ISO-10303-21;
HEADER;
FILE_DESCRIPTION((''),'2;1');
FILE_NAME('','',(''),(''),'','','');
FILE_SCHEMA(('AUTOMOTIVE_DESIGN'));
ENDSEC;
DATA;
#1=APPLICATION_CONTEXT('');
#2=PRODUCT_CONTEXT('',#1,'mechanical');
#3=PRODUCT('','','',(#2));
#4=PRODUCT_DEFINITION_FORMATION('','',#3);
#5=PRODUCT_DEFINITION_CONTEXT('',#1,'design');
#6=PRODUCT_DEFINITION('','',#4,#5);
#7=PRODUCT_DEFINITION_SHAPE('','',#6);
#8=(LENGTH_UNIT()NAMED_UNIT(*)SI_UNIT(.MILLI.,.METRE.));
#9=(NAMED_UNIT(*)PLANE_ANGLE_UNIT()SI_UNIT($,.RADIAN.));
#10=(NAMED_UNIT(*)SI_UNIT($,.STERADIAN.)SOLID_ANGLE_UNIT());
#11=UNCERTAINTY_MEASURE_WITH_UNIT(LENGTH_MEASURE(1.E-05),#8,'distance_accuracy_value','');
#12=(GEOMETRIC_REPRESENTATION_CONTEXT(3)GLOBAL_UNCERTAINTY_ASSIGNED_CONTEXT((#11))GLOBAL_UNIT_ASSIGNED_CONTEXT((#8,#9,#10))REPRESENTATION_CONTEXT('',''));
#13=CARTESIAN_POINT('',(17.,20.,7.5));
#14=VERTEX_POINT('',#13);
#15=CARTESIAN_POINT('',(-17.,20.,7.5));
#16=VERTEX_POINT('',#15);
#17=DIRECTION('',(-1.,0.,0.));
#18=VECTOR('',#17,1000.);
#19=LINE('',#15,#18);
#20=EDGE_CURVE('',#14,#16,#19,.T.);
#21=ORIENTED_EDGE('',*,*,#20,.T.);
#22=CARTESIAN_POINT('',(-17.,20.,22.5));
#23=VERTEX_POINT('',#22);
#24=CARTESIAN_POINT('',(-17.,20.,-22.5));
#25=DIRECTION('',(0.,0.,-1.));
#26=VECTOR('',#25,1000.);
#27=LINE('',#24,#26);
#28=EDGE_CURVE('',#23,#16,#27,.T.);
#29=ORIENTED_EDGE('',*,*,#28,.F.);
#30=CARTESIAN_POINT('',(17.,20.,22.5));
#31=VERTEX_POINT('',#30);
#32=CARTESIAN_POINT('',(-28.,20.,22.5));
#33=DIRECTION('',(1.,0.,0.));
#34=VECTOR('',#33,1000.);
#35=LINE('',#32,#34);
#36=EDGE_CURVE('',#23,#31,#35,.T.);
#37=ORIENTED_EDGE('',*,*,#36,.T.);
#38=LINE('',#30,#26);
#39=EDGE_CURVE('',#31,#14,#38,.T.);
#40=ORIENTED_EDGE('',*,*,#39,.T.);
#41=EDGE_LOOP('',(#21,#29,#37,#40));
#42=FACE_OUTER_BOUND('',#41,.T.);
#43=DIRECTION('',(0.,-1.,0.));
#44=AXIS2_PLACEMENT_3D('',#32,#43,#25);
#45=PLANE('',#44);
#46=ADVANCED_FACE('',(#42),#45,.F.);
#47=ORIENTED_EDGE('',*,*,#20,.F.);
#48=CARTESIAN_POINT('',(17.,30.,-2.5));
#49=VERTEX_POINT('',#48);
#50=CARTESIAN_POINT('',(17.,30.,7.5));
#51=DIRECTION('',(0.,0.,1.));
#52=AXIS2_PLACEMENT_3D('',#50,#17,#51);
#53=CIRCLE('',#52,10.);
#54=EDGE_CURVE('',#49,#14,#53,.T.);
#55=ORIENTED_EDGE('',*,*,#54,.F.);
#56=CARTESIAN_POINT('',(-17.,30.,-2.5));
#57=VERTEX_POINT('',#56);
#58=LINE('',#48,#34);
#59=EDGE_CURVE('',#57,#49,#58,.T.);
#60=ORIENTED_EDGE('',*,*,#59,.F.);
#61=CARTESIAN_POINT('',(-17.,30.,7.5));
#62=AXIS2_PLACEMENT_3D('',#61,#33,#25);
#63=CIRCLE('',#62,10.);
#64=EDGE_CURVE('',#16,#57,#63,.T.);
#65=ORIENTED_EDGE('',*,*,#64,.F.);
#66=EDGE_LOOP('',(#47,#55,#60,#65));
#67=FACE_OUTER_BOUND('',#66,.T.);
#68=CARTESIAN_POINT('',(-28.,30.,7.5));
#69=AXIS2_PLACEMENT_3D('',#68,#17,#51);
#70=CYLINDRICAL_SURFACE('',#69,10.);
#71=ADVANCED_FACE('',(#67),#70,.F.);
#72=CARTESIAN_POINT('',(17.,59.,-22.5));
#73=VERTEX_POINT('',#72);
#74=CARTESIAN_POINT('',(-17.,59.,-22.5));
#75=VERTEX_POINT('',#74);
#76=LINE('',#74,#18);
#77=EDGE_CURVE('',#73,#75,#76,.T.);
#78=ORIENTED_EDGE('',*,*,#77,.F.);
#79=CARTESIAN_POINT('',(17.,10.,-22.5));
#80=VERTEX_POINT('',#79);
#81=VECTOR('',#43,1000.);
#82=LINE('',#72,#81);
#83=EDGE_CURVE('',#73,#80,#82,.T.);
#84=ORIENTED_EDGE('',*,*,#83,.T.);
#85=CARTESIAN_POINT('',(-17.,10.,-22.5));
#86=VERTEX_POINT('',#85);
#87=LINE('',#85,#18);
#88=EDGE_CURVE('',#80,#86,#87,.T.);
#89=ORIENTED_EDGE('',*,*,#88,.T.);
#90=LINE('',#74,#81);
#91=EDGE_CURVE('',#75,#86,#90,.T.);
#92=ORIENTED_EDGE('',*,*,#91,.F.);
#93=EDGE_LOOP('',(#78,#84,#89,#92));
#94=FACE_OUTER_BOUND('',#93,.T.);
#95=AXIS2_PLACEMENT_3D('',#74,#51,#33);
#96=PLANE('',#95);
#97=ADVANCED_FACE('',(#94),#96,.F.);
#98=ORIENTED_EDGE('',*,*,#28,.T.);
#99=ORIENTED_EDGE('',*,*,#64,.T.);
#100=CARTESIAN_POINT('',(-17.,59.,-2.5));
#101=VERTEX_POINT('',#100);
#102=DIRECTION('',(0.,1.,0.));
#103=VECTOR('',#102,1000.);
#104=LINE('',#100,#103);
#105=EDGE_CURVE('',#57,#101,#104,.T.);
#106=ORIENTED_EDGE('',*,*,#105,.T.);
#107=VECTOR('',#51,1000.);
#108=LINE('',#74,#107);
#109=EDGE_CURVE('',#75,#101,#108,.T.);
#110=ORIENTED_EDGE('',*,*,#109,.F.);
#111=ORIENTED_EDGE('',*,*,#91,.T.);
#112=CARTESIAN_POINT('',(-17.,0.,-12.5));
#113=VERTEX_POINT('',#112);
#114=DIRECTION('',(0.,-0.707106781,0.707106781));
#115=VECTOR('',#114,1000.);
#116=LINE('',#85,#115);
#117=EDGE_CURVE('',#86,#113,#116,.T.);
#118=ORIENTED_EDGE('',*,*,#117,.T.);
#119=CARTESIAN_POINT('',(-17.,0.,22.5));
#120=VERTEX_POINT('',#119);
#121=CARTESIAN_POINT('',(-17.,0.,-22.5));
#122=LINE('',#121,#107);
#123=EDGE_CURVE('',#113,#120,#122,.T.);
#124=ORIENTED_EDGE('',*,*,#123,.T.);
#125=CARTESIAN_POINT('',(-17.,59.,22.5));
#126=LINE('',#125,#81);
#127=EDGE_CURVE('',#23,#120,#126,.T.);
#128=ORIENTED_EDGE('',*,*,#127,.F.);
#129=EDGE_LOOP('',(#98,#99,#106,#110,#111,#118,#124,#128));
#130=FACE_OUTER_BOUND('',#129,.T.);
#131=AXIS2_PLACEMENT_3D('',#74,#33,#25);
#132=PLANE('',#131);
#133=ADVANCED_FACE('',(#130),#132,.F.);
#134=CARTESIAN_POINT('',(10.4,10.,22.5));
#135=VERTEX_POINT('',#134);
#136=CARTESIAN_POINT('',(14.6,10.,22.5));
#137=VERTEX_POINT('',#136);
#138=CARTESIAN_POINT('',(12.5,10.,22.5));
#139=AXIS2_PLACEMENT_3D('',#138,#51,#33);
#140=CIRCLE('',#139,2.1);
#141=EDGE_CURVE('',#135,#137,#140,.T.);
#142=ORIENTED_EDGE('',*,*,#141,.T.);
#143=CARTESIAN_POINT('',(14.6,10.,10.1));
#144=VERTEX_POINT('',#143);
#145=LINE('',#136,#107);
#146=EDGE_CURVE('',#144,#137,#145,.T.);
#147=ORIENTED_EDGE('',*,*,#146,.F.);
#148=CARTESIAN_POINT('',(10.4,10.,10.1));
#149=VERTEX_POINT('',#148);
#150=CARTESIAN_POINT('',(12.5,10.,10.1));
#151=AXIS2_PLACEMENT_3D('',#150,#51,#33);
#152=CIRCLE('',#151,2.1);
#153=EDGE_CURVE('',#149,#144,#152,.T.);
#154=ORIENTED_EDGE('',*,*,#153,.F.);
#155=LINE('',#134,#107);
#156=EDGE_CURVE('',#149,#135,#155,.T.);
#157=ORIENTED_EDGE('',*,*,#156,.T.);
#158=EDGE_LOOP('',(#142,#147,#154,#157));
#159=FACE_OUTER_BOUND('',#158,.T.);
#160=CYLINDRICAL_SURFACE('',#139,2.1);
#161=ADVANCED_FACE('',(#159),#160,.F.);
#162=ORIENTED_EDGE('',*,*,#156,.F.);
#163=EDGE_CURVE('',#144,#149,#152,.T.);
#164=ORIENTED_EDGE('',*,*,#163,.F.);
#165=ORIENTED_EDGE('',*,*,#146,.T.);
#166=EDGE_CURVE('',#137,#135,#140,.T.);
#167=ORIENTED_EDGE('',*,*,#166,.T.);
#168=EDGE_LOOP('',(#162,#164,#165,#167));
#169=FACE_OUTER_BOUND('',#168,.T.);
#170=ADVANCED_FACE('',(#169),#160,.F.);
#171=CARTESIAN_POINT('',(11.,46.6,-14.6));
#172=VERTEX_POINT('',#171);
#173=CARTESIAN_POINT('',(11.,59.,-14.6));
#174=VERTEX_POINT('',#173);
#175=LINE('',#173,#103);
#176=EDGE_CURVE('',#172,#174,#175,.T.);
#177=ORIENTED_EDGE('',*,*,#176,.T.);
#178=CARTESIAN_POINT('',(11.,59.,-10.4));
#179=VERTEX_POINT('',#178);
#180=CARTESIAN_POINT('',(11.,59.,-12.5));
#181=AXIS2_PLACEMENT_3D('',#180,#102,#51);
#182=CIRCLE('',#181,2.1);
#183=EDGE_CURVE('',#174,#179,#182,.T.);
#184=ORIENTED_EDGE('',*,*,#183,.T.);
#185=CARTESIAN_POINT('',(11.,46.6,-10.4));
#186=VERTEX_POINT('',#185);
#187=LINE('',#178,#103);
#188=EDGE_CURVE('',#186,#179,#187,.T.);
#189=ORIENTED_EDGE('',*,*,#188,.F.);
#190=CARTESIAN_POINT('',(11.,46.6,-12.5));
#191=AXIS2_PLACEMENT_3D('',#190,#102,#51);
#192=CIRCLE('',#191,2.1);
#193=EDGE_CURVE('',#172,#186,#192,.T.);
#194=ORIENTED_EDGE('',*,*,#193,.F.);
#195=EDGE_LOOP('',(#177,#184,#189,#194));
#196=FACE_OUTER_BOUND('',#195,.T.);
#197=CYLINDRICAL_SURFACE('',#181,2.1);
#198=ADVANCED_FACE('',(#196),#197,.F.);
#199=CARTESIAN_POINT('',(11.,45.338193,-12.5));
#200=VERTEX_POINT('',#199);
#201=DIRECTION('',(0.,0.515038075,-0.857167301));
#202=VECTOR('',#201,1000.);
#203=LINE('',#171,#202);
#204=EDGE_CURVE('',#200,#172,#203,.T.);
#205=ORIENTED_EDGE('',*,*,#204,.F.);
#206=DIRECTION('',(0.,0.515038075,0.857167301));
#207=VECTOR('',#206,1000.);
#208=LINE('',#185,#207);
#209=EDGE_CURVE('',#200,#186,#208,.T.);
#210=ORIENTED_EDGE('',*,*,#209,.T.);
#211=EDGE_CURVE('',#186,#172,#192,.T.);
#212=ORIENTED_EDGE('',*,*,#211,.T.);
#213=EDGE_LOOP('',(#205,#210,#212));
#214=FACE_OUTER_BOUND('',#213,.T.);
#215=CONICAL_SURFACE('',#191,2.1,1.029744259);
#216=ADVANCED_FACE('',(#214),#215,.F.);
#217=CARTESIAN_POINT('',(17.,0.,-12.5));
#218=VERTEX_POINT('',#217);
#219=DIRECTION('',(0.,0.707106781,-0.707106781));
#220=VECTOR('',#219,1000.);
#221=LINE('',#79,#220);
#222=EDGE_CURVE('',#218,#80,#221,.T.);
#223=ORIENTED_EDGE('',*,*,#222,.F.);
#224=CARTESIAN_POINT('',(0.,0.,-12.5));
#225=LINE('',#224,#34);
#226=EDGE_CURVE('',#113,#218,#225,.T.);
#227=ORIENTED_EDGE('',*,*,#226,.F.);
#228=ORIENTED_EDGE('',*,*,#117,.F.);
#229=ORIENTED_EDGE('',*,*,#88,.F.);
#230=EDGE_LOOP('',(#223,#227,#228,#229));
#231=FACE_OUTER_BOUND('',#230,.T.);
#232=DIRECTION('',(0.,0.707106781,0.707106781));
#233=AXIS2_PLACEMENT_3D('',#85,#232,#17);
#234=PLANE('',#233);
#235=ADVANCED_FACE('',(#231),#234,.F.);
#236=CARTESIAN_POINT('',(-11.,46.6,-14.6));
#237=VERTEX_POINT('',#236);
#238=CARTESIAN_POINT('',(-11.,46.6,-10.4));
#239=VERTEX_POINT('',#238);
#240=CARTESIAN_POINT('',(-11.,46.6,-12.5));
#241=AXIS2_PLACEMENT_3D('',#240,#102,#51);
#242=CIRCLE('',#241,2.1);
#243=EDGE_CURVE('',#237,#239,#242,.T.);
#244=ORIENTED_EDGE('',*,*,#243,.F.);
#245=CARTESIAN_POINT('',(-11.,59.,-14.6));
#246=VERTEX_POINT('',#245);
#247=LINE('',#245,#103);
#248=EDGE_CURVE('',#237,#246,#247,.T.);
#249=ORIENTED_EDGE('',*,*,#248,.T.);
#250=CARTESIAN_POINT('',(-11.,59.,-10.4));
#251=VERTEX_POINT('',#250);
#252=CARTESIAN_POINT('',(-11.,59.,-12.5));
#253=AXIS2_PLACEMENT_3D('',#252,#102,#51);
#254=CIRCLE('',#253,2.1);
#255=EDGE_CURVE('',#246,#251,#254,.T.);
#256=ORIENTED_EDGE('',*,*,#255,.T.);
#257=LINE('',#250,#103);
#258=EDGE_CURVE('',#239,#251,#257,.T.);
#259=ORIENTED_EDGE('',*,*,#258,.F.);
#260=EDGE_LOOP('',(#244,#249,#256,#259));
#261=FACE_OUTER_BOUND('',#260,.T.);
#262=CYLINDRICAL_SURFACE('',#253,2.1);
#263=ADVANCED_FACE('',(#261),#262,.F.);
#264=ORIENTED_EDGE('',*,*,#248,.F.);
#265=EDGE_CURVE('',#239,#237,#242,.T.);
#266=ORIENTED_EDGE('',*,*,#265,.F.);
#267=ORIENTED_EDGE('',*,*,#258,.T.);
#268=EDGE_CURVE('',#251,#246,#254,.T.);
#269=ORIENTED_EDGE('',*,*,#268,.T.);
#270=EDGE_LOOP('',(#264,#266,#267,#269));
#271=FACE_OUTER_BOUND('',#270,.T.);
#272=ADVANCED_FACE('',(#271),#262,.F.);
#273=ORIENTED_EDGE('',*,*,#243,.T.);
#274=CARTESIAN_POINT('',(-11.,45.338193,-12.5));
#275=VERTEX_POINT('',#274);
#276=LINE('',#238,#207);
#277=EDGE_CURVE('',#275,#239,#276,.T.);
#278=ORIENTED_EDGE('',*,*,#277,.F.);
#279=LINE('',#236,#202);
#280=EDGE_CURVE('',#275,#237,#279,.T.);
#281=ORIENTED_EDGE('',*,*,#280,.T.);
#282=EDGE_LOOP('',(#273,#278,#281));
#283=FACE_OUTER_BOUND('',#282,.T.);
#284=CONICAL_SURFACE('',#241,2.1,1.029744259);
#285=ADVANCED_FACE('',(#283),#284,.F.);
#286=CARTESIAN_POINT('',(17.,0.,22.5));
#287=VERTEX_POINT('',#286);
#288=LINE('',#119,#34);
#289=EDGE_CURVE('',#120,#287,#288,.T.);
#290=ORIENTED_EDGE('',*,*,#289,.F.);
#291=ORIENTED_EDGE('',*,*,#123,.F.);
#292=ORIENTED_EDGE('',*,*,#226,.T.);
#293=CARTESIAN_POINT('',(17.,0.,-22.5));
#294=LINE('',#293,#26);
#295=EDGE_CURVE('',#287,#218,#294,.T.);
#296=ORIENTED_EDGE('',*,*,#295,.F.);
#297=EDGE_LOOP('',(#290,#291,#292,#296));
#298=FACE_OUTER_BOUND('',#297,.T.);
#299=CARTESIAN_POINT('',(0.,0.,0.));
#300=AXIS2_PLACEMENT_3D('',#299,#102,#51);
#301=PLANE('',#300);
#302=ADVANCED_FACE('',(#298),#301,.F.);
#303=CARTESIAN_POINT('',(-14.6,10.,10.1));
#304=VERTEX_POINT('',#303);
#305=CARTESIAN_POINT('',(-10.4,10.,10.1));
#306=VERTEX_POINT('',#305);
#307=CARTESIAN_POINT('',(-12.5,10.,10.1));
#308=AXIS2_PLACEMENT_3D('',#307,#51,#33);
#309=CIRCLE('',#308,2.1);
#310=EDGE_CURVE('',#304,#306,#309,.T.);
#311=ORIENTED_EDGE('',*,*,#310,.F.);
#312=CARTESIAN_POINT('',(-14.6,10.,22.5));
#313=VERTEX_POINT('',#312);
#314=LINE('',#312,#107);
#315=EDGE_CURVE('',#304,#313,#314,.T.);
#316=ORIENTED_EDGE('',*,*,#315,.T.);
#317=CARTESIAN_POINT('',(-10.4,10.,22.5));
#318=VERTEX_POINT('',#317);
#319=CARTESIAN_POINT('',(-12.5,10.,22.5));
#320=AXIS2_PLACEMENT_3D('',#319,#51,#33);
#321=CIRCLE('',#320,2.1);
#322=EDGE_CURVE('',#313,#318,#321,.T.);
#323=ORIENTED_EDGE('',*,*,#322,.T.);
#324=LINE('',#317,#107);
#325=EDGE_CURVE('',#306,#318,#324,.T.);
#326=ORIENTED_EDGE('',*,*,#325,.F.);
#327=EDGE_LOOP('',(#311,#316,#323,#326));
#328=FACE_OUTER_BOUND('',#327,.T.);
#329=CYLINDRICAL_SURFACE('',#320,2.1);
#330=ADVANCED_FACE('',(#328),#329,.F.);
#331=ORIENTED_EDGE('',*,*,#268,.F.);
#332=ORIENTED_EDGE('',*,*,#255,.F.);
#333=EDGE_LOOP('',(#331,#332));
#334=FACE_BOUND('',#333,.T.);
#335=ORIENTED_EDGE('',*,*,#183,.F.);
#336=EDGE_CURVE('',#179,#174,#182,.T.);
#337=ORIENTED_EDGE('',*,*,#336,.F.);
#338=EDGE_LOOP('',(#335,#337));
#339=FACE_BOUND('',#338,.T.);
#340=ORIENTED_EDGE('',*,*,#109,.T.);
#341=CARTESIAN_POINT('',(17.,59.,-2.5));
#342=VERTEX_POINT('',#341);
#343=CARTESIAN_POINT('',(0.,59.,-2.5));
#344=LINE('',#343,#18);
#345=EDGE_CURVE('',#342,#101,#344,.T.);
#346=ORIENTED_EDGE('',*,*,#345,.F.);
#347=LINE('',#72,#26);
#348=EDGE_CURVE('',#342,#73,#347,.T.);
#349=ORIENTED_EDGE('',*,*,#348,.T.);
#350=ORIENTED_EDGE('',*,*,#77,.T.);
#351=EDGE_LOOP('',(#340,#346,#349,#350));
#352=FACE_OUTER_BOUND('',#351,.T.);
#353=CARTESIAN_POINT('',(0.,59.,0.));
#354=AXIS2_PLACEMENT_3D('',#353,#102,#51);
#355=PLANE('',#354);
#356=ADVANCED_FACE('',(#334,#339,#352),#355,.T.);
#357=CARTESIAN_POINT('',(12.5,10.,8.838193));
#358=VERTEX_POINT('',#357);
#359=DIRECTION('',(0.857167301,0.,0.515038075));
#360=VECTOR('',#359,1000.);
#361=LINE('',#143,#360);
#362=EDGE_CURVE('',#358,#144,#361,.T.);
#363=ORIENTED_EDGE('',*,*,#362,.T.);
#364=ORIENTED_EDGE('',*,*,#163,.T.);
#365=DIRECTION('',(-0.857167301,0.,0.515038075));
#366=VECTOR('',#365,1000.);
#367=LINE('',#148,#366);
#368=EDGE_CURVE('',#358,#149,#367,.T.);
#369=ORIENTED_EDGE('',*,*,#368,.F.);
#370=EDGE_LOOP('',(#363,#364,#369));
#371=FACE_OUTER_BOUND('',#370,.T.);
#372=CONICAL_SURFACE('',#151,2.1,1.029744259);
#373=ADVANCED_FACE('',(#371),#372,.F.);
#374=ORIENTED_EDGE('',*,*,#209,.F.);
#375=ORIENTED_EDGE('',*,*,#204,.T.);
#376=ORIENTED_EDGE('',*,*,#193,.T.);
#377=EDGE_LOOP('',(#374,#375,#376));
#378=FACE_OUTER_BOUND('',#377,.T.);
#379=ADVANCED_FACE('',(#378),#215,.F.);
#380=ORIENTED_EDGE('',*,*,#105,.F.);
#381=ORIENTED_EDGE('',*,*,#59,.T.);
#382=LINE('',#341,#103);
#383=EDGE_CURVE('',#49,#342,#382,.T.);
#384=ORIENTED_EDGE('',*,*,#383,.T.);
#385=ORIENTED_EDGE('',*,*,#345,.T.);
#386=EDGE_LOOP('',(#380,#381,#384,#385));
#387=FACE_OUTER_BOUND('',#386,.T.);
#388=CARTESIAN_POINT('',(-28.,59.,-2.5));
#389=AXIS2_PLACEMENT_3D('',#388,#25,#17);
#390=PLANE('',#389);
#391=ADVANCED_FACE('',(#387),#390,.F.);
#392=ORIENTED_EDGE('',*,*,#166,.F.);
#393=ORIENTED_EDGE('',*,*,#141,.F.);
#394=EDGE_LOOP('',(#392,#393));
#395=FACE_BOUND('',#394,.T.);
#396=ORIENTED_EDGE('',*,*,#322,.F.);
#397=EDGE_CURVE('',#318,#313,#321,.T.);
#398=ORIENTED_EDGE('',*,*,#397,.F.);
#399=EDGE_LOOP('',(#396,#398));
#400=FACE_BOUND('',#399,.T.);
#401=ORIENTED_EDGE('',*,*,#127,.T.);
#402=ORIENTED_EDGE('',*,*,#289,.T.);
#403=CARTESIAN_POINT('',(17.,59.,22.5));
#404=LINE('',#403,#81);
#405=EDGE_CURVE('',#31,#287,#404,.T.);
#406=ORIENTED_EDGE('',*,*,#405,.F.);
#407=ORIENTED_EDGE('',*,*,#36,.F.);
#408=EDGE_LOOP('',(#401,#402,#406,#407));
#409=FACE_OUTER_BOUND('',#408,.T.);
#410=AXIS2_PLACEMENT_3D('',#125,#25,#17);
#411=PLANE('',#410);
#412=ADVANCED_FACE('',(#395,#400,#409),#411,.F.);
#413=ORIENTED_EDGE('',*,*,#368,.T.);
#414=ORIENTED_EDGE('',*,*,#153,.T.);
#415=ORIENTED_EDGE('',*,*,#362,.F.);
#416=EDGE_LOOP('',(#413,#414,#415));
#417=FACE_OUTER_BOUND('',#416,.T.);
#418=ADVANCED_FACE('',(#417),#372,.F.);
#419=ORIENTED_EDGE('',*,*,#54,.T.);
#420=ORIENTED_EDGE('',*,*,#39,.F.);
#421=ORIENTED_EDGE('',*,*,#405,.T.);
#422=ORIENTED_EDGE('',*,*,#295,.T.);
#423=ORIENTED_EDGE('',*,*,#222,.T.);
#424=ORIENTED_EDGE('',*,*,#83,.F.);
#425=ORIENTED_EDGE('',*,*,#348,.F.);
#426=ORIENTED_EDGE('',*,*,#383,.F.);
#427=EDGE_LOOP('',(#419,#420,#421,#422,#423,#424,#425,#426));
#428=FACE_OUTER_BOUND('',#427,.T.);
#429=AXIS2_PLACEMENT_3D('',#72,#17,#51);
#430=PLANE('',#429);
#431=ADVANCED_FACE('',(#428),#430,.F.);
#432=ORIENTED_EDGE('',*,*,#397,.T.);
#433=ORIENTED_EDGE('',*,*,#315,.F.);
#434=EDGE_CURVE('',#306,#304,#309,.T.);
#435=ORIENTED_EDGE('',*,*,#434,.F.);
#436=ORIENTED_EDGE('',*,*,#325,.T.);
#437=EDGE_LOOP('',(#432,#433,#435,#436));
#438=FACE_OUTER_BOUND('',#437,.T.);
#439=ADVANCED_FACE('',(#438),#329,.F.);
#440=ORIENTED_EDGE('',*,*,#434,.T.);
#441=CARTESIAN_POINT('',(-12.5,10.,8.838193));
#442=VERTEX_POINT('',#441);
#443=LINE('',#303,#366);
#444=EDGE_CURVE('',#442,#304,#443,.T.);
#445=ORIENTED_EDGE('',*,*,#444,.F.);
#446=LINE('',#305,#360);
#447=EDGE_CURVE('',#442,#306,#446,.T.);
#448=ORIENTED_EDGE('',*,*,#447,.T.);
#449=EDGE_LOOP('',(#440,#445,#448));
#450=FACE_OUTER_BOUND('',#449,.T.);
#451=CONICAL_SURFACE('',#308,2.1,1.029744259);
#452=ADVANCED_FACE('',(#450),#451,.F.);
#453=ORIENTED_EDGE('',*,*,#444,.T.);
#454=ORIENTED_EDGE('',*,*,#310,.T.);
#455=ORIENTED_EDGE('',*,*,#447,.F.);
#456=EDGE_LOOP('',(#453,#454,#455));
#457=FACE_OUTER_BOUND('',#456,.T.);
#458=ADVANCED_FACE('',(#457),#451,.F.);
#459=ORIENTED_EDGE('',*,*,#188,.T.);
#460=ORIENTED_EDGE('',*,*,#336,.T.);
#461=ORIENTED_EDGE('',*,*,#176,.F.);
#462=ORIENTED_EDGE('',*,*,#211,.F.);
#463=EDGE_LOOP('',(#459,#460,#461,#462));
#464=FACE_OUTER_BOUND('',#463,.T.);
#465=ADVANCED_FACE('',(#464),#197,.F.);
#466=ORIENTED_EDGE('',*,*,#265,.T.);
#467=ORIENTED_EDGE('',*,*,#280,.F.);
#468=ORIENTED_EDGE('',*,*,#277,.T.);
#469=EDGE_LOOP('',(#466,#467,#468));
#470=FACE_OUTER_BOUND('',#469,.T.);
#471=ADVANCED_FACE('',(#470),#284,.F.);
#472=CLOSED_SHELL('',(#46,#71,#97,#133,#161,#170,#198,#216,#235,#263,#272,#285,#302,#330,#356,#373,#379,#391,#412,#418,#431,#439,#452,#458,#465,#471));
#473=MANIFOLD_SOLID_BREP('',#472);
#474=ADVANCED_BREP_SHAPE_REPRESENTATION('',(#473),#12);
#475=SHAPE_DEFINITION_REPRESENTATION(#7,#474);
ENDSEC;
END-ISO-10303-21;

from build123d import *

# Parameters (mm, degrees)
SKETCH1_W             = 34
SKETCH1_H             = 45
BOSS_EXTRUDE1_DEPTH   = 59
SKETCH2_W             = 25
SKETCH2_H             = 39
CUT_EXTRUDE1_DEPTH    = 45
CHAMFER1_SIZE         = 10
FILLET1_R             = 10
M5_TAPPED_HOLE1_D     = 4.2
M5_TAPPED_HOLE1_DEPTH = 12.4
M5_TAPPED_HOLE1_TIP   = 1.2618073
M5_TAPPED_HOLE2_D     = 4.2
M5_TAPPED_HOLE2_DEPTH = 12.4
M5_TAPPED_HOLE2_TIP   = 1.2618073


with BuildPart() as part:
    # Sketch1 → Boss-Extrude1 (new body)
    with BuildSketch(Plane(origin=(0, 0, 0), x_dir=(1, 0, 0), z_dir=(0, 1, 0))):
        Rectangle(SKETCH1_W, SKETCH1_H)
    extrude(amount=BOSS_EXTRUDE1_DEPTH)

    # Sketch2 → Cut-Extrude1 (cut)
    with BuildSketch(Plane(origin=(17, 0, 0), x_dir=(0, 0, -1), z_dir=(1, 0, 0))):
        with Locations((-10, 39.5)):
            Rectangle(SKETCH2_W, SKETCH2_H)
    extrude(amount=-CUT_EXTRUDE1_DEPTH, mode=Mode.SUBTRACT)

    # Chamfer1
    chamfer1_edges = [part.edges().sort_by_distance(p)[0] for p in [
        (0, 0, -22.5),
    ]]
    chamfer(chamfer1_edges, length=CHAMFER1_SIZE)

    # Fillet1
    fillet1_edges = [part.edges().sort_by_distance(p)[0] for p in [
        (0, 20, -2.5),
    ]]
    fillet(fillet1_edges, radius=FILLET1_R)

    # M5 Tapped Hole1
    with Locations(Plane(origin=(-11, 59, -12.5), x_dir=(0, 0, 1), z_dir=(0, 1, 0))):
        with Locations((0, 0), (0, 22)):
            Hole(M5_TAPPED_HOLE1_D / 2, depth=M5_TAPPED_HOLE1_DEPTH)
            with Locations((0, 0, -(M5_TAPPED_HOLE1_DEPTH + M5_TAPPED_HOLE1_TIP / 2))):  # 118° drill point
                Cone(0, M5_TAPPED_HOLE1_D / 2, M5_TAPPED_HOLE1_TIP, mode=Mode.SUBTRACT)

    # M5 Tapped Hole2
    with Locations(Plane(origin=(-12.5, 10, 22.5), x_dir=(1, 0, 0), z_dir=(0, 0, 1))):
        with Locations((0, 0), (25, 0)):
            Hole(M5_TAPPED_HOLE2_D / 2, depth=M5_TAPPED_HOLE2_DEPTH)
            with Locations((0, 0, -(M5_TAPPED_HOLE2_DEPTH + M5_TAPPED_HOLE2_TIP / 2))):  # 118° drill point
                Cone(0, M5_TAPPED_HOLE2_D / 2, M5_TAPPED_HOLE2_TIP, mode=Mode.SUBTRACT)


solid = part.part
